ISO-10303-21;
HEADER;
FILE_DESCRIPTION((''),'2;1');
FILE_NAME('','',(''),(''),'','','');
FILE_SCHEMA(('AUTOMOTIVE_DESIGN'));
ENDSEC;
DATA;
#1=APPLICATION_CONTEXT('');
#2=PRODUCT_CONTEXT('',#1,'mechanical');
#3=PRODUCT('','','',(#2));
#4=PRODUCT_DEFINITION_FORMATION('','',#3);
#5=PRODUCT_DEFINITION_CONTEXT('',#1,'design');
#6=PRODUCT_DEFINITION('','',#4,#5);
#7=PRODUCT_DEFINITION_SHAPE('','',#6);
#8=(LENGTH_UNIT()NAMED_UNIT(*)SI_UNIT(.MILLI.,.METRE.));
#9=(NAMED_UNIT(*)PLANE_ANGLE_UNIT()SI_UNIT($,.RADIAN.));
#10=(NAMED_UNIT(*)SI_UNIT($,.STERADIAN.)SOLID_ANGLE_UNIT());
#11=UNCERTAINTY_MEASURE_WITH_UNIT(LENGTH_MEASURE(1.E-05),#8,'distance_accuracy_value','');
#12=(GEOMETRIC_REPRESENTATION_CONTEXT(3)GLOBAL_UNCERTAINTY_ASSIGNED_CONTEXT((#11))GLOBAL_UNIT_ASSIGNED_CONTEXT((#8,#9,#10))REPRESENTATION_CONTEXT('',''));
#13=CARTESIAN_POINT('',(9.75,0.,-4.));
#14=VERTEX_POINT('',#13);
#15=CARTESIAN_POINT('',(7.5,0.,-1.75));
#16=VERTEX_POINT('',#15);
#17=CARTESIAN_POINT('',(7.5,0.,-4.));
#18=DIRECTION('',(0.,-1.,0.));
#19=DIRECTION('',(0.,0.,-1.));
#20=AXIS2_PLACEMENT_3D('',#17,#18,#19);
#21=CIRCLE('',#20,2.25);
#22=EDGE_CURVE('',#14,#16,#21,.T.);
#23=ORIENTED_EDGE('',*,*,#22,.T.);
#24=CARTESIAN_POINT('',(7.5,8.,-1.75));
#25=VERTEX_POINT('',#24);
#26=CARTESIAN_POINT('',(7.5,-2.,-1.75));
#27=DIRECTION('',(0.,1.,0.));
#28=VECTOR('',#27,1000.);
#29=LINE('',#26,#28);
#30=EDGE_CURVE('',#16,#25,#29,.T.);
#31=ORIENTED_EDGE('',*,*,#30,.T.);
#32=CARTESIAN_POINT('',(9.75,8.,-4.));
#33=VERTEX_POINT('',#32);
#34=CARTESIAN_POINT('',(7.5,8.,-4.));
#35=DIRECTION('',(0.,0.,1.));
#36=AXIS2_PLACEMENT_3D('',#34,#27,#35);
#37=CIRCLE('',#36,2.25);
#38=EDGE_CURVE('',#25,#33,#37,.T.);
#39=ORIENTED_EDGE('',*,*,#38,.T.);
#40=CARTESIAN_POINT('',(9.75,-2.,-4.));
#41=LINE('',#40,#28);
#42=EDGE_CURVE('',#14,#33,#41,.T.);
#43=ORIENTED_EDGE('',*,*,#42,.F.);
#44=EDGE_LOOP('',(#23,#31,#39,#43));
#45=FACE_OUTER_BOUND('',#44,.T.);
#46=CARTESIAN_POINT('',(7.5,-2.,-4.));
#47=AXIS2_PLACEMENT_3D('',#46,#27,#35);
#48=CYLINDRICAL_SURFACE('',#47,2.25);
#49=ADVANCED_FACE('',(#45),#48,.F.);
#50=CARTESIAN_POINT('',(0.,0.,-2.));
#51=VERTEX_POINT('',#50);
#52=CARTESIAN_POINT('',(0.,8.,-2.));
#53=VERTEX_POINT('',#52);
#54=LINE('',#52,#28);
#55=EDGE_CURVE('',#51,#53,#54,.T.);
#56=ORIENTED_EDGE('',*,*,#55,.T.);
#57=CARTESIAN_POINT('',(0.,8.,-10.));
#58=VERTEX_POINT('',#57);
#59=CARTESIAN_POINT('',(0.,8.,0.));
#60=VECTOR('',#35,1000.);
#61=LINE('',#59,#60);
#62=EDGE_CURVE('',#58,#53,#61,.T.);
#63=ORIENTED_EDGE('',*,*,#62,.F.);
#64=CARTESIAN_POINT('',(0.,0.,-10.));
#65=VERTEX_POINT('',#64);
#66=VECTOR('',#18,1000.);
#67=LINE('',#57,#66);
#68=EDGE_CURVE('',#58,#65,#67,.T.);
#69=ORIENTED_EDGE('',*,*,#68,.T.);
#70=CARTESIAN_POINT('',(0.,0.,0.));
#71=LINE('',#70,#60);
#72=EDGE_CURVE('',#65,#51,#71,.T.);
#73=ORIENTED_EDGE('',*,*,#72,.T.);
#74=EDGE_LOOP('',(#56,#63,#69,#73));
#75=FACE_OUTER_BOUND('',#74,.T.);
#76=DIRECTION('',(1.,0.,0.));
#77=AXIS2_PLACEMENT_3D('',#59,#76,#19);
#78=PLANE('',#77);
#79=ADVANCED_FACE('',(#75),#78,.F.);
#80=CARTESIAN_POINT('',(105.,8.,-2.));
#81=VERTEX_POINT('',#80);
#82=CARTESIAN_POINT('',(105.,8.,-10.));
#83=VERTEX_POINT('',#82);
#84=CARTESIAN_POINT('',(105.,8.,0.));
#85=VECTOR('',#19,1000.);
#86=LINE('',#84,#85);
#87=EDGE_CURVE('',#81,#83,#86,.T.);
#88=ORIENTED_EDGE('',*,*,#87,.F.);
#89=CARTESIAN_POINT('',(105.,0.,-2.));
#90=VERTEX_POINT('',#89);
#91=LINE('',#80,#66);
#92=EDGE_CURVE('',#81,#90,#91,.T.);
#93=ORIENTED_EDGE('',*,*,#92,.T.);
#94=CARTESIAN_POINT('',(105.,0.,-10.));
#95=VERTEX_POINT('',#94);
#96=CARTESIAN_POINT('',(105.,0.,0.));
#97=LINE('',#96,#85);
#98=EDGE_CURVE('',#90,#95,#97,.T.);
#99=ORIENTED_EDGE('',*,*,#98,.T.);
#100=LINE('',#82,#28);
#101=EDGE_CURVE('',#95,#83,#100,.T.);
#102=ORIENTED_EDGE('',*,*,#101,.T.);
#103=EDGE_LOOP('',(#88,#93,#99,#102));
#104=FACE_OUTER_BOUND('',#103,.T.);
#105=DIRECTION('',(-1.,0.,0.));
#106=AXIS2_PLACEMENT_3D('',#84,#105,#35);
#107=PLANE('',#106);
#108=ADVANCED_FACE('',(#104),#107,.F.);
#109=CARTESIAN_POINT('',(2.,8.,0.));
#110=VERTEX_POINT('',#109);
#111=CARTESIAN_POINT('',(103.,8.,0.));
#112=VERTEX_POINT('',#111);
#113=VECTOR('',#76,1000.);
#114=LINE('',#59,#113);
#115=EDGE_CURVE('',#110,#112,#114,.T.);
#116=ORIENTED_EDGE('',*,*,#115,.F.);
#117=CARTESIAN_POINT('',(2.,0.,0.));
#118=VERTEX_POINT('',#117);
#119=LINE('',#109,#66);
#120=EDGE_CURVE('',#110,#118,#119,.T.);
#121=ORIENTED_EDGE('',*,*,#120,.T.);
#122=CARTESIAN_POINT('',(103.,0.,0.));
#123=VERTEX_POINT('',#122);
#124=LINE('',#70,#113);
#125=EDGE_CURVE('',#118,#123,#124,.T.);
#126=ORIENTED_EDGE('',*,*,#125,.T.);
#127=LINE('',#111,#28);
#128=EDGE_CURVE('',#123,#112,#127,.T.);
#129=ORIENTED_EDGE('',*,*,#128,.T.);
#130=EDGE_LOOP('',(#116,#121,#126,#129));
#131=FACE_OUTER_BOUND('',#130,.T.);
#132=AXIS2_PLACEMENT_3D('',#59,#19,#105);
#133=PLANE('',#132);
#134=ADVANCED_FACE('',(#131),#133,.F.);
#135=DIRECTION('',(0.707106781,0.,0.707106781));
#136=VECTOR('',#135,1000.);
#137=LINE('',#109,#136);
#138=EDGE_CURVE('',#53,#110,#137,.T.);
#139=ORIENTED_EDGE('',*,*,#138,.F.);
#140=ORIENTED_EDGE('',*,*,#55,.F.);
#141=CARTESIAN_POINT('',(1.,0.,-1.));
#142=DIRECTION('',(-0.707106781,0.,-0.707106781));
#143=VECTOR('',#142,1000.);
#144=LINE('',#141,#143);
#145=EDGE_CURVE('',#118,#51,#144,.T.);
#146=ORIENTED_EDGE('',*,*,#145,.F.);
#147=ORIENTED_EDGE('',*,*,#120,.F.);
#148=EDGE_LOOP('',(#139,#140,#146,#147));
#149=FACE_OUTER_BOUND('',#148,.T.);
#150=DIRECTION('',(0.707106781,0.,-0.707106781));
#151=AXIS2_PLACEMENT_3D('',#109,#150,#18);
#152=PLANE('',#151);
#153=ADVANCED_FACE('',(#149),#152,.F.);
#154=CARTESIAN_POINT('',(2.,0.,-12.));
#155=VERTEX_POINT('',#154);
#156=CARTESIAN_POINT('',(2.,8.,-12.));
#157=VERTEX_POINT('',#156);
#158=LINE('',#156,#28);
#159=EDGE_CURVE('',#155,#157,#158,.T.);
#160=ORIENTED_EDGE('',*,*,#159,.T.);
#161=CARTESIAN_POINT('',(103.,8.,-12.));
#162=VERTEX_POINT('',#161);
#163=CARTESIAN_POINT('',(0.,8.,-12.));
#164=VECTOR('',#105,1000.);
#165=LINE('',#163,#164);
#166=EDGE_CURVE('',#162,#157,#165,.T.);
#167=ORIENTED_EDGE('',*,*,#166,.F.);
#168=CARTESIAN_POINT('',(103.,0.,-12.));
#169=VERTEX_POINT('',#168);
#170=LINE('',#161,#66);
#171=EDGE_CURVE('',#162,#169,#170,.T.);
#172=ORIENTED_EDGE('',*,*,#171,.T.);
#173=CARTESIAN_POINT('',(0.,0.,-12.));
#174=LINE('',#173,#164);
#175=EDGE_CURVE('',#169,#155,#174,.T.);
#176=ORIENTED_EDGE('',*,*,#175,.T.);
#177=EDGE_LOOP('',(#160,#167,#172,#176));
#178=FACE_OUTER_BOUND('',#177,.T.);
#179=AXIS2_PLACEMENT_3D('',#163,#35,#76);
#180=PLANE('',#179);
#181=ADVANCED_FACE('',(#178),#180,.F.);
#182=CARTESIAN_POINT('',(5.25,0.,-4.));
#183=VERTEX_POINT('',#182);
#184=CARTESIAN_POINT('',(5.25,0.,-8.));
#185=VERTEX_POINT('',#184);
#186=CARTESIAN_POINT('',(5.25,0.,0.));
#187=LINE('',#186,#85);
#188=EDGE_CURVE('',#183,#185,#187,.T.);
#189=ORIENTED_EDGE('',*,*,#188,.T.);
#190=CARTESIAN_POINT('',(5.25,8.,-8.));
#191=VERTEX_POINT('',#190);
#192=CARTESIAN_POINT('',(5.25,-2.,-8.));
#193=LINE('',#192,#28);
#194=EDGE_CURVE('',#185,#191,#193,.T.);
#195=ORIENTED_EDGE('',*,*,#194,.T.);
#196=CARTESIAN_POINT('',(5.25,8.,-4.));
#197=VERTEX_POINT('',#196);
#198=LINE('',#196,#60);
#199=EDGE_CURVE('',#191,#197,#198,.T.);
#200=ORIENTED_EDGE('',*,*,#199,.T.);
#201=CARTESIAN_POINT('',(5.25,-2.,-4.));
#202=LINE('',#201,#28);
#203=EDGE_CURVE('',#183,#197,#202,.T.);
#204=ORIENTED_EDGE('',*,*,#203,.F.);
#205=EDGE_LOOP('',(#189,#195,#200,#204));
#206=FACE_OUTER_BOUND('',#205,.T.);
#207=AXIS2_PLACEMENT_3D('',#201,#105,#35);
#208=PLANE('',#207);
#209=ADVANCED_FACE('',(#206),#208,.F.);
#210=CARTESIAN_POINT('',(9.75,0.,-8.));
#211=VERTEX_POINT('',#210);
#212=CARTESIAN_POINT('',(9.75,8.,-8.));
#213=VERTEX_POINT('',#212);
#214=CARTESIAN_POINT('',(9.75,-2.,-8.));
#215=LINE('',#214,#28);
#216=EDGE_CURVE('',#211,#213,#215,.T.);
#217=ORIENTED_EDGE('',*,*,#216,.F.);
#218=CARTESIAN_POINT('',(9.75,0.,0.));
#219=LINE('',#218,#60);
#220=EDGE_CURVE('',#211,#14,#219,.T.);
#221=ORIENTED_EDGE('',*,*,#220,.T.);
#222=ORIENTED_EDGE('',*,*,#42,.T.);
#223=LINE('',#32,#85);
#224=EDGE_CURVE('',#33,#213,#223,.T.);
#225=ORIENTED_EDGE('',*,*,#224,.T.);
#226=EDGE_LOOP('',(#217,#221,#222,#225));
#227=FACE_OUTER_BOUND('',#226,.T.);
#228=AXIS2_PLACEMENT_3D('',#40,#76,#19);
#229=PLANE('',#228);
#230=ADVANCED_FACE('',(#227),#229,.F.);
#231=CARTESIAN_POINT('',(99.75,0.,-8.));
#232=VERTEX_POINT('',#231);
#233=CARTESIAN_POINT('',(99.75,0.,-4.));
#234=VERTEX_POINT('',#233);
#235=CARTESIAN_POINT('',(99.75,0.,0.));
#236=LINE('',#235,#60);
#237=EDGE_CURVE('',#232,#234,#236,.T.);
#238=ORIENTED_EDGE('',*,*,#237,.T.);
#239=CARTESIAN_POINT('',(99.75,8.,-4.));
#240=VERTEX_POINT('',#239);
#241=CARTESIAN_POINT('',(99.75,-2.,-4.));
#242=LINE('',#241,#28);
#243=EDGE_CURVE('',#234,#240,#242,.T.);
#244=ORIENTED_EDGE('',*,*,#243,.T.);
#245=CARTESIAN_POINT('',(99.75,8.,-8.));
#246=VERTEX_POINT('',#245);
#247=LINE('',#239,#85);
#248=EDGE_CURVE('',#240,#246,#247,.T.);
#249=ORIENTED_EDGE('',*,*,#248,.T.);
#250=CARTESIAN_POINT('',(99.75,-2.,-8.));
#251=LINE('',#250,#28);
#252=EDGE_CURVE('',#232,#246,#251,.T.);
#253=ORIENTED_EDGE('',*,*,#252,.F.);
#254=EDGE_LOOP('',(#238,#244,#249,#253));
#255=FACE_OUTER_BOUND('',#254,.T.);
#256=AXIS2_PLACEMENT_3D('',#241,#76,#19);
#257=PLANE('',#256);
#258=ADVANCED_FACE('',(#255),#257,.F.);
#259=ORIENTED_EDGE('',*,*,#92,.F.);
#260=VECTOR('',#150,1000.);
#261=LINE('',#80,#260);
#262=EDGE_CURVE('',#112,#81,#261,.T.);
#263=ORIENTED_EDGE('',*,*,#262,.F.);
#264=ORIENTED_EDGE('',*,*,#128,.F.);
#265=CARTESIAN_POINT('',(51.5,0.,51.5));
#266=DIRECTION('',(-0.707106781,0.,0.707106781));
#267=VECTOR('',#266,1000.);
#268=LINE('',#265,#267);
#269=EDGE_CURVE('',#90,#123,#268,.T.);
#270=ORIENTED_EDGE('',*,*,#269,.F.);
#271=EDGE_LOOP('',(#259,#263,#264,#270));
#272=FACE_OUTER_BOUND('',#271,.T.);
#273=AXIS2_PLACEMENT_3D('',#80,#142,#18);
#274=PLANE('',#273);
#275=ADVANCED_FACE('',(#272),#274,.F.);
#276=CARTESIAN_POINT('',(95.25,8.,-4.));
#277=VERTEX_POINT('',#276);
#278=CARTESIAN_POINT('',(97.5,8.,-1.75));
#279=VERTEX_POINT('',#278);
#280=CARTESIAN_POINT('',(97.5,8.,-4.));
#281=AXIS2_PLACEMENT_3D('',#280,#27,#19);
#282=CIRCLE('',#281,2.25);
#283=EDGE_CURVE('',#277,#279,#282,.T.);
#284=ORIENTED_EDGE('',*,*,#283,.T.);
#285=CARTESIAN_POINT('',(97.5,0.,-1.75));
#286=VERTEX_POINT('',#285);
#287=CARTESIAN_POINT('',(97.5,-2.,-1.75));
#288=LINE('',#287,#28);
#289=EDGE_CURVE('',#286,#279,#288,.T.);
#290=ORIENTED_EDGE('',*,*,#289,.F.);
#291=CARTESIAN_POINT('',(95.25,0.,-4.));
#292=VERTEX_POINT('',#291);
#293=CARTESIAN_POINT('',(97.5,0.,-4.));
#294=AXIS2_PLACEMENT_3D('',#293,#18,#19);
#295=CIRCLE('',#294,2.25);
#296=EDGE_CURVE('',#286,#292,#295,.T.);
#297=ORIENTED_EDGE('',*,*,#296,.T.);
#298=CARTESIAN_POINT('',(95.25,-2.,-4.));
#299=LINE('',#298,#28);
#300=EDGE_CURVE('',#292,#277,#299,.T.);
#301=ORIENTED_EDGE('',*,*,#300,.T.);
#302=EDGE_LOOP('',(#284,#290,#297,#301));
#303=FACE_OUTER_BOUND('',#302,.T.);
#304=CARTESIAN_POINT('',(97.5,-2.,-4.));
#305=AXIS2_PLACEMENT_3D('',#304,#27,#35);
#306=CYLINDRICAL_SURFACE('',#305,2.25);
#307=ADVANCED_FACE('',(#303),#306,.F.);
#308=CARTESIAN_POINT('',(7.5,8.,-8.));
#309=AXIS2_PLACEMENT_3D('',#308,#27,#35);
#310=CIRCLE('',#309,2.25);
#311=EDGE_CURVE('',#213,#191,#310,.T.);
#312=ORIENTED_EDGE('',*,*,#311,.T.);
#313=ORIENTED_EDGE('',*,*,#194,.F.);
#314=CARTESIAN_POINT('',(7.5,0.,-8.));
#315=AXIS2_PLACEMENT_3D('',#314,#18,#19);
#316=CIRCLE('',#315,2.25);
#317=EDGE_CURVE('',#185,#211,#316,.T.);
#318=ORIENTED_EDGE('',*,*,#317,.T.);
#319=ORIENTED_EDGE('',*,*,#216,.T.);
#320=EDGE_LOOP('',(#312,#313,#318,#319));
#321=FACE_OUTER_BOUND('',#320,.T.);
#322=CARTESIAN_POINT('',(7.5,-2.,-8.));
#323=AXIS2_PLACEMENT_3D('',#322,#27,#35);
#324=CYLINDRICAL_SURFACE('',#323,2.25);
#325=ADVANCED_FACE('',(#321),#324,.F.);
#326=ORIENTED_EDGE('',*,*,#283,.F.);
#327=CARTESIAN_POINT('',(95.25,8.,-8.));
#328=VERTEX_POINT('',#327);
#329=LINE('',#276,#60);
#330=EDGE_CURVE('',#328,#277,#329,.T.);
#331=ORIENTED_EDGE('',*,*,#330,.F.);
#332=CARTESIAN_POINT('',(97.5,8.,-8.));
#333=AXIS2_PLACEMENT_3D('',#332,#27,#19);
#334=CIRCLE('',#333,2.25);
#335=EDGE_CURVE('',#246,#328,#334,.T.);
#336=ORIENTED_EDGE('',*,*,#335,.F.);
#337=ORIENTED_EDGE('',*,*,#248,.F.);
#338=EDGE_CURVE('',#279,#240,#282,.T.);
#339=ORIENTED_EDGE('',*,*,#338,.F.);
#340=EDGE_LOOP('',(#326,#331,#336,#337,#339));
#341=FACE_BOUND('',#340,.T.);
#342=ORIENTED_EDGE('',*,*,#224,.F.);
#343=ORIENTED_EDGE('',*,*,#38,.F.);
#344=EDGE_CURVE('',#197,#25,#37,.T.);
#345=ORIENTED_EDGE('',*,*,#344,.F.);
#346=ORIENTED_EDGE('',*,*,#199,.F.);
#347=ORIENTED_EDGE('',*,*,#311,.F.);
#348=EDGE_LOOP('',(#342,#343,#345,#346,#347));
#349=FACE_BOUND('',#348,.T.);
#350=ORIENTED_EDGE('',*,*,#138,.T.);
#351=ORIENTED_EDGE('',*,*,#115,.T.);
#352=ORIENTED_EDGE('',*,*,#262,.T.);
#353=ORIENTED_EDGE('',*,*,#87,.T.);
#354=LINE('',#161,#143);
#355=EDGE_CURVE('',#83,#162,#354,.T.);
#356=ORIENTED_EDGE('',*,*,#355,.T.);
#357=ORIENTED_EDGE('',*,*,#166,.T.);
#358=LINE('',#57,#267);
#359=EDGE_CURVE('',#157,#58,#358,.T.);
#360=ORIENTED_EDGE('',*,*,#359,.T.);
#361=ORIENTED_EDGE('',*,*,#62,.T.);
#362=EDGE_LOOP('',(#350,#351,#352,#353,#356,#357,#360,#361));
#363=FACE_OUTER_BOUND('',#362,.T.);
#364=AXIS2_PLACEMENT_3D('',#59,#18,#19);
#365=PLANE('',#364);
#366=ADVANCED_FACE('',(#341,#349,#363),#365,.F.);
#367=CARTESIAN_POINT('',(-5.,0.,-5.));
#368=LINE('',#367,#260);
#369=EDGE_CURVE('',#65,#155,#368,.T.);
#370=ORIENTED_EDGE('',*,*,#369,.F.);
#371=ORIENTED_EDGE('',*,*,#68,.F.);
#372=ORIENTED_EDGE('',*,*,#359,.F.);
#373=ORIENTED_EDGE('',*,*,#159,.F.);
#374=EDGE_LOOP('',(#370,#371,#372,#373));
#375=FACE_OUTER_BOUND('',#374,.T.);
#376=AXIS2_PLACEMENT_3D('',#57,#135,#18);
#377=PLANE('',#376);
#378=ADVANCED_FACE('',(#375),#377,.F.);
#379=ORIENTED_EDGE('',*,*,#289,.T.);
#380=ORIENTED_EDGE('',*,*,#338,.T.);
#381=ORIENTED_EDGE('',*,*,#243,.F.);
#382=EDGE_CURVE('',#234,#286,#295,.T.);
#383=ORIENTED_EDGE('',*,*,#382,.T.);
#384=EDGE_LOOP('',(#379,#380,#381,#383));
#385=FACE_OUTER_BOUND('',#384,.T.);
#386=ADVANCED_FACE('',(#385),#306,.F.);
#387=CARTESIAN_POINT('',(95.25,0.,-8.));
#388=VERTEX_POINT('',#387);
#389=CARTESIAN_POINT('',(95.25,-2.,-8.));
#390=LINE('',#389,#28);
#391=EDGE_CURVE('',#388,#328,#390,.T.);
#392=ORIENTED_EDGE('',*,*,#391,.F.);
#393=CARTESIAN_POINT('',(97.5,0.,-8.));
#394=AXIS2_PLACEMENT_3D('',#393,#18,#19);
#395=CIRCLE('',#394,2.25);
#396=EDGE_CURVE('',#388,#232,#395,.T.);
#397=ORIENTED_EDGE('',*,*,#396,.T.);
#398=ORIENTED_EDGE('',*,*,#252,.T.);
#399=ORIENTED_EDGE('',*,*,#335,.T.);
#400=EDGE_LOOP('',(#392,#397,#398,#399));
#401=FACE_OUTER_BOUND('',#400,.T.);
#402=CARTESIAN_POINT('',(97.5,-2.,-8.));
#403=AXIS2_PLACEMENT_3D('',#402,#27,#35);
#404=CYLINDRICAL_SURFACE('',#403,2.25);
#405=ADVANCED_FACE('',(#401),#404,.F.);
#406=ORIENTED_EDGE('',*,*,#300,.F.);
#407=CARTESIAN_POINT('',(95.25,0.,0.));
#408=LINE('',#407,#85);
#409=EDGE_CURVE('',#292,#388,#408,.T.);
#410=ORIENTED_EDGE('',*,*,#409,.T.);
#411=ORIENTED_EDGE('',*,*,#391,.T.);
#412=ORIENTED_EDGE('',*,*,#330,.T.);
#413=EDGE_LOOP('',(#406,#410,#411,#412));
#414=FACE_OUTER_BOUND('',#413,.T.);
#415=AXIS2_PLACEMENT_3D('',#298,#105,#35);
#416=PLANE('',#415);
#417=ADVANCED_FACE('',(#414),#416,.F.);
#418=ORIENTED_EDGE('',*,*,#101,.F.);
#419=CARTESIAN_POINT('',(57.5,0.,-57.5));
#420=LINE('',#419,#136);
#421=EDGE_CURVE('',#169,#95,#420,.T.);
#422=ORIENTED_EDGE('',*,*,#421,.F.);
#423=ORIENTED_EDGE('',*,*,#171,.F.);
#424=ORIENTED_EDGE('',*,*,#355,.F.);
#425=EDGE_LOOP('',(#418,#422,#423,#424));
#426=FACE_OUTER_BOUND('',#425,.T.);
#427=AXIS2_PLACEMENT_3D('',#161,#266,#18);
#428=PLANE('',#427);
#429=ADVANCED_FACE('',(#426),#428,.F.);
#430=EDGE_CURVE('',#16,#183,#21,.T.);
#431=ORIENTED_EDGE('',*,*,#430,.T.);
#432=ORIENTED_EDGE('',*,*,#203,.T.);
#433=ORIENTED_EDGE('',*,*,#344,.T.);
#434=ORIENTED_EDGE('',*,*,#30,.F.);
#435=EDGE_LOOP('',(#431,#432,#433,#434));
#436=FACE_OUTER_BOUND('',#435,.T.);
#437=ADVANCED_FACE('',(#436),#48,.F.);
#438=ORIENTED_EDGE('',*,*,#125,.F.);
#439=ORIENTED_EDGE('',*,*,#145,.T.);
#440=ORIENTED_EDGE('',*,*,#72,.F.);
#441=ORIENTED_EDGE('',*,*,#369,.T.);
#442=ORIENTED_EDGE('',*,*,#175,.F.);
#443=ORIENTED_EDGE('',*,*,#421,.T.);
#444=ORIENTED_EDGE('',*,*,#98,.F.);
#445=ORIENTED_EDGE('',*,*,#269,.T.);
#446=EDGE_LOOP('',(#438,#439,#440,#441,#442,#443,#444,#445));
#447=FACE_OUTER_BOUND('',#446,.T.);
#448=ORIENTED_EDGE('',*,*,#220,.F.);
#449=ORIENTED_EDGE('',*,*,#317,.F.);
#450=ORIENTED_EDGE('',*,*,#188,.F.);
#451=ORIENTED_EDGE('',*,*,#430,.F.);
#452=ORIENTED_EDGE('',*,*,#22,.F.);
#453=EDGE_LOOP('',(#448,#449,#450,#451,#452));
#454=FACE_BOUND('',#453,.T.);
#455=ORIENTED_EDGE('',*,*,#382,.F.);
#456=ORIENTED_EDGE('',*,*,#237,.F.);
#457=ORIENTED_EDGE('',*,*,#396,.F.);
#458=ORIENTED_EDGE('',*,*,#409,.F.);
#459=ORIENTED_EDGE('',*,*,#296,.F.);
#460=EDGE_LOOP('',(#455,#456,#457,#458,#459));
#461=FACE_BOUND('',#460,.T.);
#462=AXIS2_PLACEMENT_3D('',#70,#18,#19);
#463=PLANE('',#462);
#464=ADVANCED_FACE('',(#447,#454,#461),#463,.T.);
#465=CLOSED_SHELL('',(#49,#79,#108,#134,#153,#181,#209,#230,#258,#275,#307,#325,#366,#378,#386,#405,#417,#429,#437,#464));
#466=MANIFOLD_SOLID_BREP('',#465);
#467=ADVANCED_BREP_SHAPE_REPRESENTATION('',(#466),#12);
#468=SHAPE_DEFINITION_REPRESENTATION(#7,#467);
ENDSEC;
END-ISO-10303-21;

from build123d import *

# Parameters (mm, degrees)
SKETCH1_W           = 105
SKETCH1_H           = 12
BOSS_EXTRUDE1_DEPTH = 8
CHAMFER1_SIZE       = 2
SKETCH2_R           = 2.25
CUT_EXTRUDE1_DEPTH  = 10
CUT_EXTRUDE2_DEPTH  = 10


with BuildPart() as part:
    # Sketch1 → Boss-Extrude1 (new body)
    with BuildSketch(Plane(origin=(0, 0, 0), x_dir=(1, 0, 0), z_dir=(0, 1, 0))):
        with Locations((52.5, 6)):
            Rectangle(SKETCH1_W, SKETCH1_H)
    extrude(amount=BOSS_EXTRUDE1_DEPTH)

    # Chamfer1
    chamfer1_edges = [part.edges().sort_by_distance(p)[0] for p in [
        (0, 4, -12),
        (105, 4, -12),
        (105, 4, 0),
        (0, 4, 0),
    ]]
    chamfer(chamfer1_edges, length=CHAMFER1_SIZE)

    # Sketch2 → Cut-Extrude1 (cut)
    with BuildSketch(Plane(origin=(0, 8, 0), x_dir=(1, 0, 0), z_dir=(0, 1, 0))):
        with Locations(Location((7.5, 6, 0), (0, 0, 270))):
            Circle(SKETCH2_R)
        with Locations(Location((97.5, 6, 0), (0, 0, 90))):
            Circle(SKETCH2_R)
    extrude(amount=-CUT_EXTRUDE1_DEPTH, mode=Mode.SUBTRACT)

    # Sketch3 → Cut-Extrude2 (cut)
    with BuildSketch(Plane(origin=(0, 8, 0), x_dir=(1, 0, 0), z_dir=(0, 1, 0))):
        with BuildLine():
            Line((5.25, 4), (5.25, 8))
            ThreePointArc((5.25, 8), (7.5, 10.25), (9.75, 8))
            Line((9.75, 8), (9.75, 4))
            ThreePointArc((9.75, 4), (7.5, 1.75), (5.25, 4))
        make_face()
        with BuildLine():
            Line((99.75, 4), (99.75, 8))
            ThreePointArc((99.75, 8), (97.5, 10.25), (95.25, 8))
            Line((95.25, 8), (95.25, 4))
            ThreePointArc((95.25, 4), (97.5, 1.75), (99.75, 4))
        make_face()
    extrude(amount=-CUT_EXTRUDE2_DEPTH, mode=Mode.SUBTRACT)


solid = part.part
